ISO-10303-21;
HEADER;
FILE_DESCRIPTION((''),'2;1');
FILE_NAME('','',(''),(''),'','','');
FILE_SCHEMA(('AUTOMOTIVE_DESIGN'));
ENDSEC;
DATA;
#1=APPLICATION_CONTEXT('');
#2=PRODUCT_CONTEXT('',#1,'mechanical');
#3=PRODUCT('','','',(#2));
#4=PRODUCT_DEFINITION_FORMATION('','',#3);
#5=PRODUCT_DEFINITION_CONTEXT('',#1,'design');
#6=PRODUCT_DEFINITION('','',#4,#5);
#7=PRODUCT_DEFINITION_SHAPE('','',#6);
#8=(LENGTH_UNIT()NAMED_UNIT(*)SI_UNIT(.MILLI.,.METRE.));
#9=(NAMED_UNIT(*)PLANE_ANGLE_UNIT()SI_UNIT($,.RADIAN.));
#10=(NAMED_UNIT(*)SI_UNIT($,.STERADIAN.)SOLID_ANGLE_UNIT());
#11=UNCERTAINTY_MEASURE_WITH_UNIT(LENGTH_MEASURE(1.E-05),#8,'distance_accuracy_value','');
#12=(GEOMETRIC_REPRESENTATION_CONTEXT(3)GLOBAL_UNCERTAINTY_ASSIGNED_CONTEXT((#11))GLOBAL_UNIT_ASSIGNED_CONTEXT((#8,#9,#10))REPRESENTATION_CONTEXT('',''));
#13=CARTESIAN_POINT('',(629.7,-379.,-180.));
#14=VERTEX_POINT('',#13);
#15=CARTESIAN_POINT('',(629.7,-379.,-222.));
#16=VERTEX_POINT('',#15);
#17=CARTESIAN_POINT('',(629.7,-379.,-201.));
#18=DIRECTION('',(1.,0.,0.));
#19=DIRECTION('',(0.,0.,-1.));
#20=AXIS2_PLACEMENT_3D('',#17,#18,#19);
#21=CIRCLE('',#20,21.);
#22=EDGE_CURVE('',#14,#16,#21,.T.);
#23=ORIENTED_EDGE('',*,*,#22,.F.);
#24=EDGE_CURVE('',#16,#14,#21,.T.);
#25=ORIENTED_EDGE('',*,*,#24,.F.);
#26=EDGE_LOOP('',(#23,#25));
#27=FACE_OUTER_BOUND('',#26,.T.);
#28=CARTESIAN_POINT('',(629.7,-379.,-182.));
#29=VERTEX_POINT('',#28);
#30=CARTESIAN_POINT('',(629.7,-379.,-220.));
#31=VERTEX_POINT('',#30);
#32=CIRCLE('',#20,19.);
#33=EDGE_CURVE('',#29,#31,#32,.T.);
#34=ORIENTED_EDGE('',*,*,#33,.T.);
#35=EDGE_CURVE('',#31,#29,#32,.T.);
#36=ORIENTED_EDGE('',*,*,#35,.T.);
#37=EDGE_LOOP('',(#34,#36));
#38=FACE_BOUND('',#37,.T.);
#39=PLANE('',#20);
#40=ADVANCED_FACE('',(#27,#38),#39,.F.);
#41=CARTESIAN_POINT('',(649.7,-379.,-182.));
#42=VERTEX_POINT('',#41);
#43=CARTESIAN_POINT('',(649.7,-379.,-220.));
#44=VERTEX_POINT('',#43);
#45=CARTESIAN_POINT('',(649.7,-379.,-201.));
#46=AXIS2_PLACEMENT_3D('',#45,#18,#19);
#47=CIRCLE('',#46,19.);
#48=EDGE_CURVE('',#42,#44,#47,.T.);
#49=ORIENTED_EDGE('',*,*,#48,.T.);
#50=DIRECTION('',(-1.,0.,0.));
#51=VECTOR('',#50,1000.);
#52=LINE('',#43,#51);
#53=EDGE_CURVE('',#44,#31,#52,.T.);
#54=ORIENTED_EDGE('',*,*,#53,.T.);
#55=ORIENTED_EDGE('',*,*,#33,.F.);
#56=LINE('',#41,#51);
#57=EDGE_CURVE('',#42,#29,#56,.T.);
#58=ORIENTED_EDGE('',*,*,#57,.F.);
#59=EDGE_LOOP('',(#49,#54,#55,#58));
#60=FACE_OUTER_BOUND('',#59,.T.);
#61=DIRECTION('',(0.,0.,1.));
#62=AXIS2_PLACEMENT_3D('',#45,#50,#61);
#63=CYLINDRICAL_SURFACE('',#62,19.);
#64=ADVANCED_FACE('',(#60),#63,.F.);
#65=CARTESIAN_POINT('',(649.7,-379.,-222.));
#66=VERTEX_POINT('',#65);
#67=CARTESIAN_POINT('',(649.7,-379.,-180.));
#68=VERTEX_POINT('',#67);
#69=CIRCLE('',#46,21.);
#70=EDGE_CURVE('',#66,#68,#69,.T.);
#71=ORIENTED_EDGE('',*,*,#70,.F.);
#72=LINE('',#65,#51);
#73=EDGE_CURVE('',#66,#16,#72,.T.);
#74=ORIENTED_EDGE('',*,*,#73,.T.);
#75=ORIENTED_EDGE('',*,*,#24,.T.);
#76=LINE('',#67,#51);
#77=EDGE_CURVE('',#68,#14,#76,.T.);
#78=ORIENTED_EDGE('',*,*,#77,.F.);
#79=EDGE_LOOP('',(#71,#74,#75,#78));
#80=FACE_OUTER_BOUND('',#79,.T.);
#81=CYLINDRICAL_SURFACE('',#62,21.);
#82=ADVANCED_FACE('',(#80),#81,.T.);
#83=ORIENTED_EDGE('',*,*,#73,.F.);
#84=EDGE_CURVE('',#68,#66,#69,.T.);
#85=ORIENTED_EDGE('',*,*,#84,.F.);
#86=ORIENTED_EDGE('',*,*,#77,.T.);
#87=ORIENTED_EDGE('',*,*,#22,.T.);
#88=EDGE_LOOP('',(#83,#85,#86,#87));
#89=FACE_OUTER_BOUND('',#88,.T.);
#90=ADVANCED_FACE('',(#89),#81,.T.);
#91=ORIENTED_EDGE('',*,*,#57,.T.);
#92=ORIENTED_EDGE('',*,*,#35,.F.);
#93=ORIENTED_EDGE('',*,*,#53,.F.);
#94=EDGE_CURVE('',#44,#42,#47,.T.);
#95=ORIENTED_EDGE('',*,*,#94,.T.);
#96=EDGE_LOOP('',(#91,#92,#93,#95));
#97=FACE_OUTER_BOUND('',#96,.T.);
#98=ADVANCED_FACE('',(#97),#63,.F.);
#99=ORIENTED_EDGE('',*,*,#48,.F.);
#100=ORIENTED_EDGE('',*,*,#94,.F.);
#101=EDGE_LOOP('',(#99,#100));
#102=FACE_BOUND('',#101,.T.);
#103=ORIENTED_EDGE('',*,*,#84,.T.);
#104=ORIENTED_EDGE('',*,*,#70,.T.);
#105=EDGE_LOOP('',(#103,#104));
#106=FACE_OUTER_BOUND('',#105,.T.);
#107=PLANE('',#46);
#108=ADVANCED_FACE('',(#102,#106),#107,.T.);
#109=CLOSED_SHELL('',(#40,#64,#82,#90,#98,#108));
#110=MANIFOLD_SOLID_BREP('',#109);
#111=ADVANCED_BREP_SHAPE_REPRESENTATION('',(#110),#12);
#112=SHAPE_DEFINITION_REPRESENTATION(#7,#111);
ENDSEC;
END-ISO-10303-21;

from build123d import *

# Parameters (mm, degrees)
SKETCH_1_R      = 21
SKETCH_1_R_2    = 19
EXTRUDE_1_DEPTH = 20


with BuildPart() as part:
    # 草图1 → 凸台-拉伸1 (new body)
    with BuildSketch(Plane(origin=(629.7, 0, 0), x_dir=(0, 0, -1), z_dir=(1, 0, 0))):
        with Locations((201, -379)):
            Circle(SKETCH_1_R)
        with Locations((201, -379)):
            Circle(SKETCH_1_R_2, mode=Mode.SUBTRACT)
    extrude(amount=EXTRUDE_1_DEPTH)


solid = part.part
